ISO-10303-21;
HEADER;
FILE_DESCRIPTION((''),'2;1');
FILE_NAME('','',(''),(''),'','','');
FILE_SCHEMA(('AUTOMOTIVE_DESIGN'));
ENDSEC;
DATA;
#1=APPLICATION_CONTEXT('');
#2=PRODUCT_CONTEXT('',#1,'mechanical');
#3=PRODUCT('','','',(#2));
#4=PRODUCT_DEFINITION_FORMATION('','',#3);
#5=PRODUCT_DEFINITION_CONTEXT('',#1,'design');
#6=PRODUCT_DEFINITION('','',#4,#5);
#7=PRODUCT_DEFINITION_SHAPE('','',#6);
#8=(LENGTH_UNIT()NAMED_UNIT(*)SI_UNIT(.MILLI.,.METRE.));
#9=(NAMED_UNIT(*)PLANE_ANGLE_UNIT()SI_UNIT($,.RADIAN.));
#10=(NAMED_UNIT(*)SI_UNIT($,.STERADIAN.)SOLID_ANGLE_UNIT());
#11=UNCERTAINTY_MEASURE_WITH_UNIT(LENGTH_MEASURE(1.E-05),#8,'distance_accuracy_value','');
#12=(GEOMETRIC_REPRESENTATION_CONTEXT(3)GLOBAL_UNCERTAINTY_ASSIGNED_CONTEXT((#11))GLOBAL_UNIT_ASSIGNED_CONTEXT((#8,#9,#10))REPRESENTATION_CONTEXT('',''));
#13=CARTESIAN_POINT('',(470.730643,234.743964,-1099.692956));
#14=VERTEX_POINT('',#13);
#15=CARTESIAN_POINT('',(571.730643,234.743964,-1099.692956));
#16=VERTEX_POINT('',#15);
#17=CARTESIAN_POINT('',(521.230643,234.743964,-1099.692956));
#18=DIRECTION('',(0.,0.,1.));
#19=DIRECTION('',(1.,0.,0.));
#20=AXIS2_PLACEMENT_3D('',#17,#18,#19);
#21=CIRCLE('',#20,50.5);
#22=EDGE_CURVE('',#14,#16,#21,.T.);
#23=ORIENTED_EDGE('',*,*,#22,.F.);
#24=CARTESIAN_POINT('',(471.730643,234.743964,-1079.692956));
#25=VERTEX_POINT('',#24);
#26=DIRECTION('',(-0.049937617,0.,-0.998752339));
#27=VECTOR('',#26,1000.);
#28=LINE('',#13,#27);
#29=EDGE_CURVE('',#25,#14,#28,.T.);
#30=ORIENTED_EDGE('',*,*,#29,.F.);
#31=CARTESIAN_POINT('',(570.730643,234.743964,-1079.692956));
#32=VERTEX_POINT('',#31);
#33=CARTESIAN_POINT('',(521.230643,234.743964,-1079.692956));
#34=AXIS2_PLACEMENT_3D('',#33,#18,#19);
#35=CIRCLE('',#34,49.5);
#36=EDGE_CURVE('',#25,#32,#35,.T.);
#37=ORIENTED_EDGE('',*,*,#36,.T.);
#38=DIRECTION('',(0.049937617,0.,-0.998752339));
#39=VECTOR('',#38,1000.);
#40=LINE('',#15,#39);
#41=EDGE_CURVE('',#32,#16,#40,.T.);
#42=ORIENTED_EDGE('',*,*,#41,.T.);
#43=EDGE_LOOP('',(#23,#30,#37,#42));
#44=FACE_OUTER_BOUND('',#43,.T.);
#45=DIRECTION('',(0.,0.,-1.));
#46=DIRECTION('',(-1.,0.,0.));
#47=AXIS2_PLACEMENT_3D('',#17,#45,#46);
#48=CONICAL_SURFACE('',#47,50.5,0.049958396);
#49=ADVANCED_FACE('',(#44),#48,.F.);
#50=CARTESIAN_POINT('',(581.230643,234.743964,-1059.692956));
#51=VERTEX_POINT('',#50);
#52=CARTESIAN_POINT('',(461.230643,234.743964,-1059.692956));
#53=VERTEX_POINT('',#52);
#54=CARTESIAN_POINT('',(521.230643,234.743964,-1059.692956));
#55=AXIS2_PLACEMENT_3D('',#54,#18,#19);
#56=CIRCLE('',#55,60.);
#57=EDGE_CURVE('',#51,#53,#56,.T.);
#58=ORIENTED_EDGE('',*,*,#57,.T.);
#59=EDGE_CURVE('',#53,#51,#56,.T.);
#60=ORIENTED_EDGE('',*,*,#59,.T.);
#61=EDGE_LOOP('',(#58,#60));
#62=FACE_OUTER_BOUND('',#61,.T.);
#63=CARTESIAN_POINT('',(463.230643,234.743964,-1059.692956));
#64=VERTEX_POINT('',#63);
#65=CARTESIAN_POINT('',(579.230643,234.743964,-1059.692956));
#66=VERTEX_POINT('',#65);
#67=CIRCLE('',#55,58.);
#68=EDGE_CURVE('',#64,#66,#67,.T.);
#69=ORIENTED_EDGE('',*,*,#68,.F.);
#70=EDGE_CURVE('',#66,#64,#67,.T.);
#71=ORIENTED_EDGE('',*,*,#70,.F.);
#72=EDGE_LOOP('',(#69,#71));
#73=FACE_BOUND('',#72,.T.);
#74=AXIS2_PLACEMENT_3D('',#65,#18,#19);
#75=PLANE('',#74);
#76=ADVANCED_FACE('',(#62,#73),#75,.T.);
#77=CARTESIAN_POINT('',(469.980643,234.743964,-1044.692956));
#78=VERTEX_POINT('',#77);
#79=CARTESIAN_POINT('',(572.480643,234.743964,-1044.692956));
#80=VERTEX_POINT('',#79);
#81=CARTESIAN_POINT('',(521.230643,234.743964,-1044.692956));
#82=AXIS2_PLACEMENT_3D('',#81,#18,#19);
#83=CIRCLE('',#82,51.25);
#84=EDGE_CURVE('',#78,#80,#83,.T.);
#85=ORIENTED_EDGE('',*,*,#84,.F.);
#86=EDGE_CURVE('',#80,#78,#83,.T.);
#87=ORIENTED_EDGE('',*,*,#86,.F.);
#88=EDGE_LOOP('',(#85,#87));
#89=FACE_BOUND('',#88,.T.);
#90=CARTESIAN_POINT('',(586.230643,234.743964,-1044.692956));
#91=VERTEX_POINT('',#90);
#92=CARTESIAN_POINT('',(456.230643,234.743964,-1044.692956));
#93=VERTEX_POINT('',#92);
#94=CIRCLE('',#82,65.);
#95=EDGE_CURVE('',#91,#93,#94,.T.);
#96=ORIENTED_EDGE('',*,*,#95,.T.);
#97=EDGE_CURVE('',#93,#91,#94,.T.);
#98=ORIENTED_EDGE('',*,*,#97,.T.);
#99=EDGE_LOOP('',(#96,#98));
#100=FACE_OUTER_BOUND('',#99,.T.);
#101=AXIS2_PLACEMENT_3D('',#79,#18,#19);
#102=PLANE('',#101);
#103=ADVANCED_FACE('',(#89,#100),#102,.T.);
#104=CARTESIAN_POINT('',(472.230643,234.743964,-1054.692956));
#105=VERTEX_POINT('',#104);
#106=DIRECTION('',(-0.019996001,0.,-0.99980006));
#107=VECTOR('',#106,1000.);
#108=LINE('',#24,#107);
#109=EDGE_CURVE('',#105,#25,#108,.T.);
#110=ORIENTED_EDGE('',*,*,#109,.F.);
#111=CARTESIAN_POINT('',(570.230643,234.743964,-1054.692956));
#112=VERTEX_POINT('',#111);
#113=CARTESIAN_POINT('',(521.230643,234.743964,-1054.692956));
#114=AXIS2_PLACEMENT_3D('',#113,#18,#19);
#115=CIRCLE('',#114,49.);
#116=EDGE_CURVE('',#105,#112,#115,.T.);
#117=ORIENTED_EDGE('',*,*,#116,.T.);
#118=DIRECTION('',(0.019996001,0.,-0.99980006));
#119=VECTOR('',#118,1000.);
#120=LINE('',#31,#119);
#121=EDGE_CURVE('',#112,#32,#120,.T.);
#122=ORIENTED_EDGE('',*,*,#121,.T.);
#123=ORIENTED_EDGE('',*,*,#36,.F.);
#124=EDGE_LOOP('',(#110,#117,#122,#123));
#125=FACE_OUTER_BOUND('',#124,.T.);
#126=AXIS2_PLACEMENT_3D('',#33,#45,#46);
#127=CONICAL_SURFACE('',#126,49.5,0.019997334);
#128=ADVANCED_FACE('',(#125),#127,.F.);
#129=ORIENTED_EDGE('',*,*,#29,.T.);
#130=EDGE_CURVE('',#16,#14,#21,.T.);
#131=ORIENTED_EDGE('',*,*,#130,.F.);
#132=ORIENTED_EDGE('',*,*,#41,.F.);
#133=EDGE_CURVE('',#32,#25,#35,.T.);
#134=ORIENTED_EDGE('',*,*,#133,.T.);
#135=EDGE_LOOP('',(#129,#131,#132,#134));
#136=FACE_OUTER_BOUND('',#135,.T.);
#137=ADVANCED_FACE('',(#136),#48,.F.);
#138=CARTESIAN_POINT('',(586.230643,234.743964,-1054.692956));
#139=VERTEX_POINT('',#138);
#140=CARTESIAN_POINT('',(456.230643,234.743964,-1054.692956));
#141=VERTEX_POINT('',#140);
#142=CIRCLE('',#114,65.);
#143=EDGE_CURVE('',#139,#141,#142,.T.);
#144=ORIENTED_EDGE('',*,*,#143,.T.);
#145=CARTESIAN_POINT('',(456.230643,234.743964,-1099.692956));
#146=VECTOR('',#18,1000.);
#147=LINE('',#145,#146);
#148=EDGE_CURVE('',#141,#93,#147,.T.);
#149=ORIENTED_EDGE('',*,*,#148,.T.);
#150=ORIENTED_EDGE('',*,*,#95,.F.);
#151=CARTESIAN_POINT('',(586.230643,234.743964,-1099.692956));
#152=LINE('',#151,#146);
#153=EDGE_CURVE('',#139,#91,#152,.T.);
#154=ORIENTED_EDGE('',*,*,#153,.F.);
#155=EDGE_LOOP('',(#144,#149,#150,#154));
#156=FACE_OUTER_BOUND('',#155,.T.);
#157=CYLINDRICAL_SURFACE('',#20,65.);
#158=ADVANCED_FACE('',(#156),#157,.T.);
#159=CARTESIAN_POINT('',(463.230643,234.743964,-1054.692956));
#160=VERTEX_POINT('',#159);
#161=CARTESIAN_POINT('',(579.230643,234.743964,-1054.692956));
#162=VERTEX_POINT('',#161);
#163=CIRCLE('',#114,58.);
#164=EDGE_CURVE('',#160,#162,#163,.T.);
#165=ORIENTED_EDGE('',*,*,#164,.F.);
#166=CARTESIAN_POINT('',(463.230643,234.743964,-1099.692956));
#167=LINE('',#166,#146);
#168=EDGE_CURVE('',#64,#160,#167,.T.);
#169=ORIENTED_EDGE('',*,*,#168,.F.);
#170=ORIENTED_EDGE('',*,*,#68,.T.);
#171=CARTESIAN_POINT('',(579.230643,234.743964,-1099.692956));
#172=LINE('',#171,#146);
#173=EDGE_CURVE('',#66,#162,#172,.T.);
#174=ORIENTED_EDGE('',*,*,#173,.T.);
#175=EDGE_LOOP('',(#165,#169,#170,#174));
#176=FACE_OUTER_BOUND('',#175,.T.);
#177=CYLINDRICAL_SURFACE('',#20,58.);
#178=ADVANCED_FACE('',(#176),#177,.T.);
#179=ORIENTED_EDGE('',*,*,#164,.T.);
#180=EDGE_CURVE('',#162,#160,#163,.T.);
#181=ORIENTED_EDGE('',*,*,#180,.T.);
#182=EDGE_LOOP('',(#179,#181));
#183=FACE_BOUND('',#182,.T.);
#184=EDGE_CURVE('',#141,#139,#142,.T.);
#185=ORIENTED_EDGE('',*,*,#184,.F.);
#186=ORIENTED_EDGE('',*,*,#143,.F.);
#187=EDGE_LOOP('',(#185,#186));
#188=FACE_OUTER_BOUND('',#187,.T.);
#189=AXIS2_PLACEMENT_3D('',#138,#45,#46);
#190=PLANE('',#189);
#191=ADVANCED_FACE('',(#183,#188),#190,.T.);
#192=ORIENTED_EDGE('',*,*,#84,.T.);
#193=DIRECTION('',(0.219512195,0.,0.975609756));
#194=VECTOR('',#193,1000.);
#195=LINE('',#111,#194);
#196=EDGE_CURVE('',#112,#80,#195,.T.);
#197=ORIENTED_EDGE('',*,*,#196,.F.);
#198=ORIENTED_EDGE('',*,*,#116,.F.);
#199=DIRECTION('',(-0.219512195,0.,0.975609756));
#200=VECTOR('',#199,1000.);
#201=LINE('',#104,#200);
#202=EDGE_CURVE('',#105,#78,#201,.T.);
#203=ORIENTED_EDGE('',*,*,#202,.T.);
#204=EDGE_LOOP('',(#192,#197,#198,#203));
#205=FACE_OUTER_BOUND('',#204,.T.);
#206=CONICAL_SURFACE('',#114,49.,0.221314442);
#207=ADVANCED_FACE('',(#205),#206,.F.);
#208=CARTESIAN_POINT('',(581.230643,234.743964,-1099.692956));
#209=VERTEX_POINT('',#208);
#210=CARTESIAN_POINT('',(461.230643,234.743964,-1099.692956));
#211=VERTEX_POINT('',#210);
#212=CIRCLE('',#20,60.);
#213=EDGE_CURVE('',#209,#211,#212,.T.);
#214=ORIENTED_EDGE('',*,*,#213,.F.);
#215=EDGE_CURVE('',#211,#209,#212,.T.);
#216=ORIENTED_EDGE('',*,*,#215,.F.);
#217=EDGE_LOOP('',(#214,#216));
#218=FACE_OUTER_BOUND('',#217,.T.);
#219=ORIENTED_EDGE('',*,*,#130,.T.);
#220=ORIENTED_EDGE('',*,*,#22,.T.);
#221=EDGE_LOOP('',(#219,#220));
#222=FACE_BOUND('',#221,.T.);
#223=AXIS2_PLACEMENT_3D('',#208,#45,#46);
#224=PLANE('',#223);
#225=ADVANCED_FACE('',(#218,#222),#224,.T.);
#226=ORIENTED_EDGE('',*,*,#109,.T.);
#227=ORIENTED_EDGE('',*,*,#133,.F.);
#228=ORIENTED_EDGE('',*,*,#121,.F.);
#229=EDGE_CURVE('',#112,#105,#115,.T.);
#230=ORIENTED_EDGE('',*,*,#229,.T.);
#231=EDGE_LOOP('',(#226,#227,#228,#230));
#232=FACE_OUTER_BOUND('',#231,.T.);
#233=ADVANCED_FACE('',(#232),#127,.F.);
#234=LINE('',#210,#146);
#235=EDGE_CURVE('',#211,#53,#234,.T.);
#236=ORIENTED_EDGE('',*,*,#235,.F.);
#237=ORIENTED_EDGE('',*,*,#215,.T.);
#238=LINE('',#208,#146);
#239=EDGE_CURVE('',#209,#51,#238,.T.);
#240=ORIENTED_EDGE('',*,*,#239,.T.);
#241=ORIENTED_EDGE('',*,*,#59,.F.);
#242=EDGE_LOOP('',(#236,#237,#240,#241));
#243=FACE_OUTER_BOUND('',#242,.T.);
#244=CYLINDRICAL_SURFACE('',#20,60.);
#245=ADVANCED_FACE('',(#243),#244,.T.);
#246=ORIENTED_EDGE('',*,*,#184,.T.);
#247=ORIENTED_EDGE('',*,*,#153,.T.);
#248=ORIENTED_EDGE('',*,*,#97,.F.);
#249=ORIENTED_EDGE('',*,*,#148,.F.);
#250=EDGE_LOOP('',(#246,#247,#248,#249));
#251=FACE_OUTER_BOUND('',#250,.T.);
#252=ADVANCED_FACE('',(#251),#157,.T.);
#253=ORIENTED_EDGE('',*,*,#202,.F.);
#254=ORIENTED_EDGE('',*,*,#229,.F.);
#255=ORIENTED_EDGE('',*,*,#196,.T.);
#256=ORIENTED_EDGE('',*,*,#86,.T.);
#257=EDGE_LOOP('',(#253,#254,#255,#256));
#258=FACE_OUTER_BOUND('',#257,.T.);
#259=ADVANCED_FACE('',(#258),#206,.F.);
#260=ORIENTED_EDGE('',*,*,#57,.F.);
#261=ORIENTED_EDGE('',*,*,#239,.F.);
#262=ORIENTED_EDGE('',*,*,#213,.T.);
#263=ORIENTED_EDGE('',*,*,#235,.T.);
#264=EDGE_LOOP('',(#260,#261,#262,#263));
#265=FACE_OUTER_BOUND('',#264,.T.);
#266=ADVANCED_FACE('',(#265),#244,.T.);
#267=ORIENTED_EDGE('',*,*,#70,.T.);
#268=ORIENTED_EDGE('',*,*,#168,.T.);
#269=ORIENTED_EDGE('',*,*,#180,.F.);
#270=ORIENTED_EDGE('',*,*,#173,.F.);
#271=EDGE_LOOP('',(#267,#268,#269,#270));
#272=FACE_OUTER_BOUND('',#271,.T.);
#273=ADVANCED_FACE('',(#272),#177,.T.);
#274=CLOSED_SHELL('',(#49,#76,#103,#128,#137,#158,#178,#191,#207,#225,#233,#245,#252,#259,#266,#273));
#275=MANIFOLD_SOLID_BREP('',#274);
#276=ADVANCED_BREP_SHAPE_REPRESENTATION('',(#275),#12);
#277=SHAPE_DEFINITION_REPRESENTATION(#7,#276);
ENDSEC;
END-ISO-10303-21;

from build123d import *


with BuildPart() as part:
    # Sketch1 → Revolve1 (revolve)
    with BuildSketch(Plane(origin=(0, 234.743963655, 0), x_dir=(1, 0, 0), z_dir=(0, 1, 0))):
        Polygon((586.230642584, 1054.692956355), (579.230642584, 1054.692956355), (579.230642584, 1059.692956355), (581.230642584, 1059.692956355), (581.230642584, 1099.692956355), (571.730642584, 1099.692956355), (570.730642584, 1079.692956355), (570.230642584, 1054.692956355), (572.480642584, 1044.692956355), (586.230642584, 1044.692956355), align=None)
    revolve(axis=Axis((521.230642584, 234.743963655, -1099.692956355), (0, 0, 1)))


solid = part.part
